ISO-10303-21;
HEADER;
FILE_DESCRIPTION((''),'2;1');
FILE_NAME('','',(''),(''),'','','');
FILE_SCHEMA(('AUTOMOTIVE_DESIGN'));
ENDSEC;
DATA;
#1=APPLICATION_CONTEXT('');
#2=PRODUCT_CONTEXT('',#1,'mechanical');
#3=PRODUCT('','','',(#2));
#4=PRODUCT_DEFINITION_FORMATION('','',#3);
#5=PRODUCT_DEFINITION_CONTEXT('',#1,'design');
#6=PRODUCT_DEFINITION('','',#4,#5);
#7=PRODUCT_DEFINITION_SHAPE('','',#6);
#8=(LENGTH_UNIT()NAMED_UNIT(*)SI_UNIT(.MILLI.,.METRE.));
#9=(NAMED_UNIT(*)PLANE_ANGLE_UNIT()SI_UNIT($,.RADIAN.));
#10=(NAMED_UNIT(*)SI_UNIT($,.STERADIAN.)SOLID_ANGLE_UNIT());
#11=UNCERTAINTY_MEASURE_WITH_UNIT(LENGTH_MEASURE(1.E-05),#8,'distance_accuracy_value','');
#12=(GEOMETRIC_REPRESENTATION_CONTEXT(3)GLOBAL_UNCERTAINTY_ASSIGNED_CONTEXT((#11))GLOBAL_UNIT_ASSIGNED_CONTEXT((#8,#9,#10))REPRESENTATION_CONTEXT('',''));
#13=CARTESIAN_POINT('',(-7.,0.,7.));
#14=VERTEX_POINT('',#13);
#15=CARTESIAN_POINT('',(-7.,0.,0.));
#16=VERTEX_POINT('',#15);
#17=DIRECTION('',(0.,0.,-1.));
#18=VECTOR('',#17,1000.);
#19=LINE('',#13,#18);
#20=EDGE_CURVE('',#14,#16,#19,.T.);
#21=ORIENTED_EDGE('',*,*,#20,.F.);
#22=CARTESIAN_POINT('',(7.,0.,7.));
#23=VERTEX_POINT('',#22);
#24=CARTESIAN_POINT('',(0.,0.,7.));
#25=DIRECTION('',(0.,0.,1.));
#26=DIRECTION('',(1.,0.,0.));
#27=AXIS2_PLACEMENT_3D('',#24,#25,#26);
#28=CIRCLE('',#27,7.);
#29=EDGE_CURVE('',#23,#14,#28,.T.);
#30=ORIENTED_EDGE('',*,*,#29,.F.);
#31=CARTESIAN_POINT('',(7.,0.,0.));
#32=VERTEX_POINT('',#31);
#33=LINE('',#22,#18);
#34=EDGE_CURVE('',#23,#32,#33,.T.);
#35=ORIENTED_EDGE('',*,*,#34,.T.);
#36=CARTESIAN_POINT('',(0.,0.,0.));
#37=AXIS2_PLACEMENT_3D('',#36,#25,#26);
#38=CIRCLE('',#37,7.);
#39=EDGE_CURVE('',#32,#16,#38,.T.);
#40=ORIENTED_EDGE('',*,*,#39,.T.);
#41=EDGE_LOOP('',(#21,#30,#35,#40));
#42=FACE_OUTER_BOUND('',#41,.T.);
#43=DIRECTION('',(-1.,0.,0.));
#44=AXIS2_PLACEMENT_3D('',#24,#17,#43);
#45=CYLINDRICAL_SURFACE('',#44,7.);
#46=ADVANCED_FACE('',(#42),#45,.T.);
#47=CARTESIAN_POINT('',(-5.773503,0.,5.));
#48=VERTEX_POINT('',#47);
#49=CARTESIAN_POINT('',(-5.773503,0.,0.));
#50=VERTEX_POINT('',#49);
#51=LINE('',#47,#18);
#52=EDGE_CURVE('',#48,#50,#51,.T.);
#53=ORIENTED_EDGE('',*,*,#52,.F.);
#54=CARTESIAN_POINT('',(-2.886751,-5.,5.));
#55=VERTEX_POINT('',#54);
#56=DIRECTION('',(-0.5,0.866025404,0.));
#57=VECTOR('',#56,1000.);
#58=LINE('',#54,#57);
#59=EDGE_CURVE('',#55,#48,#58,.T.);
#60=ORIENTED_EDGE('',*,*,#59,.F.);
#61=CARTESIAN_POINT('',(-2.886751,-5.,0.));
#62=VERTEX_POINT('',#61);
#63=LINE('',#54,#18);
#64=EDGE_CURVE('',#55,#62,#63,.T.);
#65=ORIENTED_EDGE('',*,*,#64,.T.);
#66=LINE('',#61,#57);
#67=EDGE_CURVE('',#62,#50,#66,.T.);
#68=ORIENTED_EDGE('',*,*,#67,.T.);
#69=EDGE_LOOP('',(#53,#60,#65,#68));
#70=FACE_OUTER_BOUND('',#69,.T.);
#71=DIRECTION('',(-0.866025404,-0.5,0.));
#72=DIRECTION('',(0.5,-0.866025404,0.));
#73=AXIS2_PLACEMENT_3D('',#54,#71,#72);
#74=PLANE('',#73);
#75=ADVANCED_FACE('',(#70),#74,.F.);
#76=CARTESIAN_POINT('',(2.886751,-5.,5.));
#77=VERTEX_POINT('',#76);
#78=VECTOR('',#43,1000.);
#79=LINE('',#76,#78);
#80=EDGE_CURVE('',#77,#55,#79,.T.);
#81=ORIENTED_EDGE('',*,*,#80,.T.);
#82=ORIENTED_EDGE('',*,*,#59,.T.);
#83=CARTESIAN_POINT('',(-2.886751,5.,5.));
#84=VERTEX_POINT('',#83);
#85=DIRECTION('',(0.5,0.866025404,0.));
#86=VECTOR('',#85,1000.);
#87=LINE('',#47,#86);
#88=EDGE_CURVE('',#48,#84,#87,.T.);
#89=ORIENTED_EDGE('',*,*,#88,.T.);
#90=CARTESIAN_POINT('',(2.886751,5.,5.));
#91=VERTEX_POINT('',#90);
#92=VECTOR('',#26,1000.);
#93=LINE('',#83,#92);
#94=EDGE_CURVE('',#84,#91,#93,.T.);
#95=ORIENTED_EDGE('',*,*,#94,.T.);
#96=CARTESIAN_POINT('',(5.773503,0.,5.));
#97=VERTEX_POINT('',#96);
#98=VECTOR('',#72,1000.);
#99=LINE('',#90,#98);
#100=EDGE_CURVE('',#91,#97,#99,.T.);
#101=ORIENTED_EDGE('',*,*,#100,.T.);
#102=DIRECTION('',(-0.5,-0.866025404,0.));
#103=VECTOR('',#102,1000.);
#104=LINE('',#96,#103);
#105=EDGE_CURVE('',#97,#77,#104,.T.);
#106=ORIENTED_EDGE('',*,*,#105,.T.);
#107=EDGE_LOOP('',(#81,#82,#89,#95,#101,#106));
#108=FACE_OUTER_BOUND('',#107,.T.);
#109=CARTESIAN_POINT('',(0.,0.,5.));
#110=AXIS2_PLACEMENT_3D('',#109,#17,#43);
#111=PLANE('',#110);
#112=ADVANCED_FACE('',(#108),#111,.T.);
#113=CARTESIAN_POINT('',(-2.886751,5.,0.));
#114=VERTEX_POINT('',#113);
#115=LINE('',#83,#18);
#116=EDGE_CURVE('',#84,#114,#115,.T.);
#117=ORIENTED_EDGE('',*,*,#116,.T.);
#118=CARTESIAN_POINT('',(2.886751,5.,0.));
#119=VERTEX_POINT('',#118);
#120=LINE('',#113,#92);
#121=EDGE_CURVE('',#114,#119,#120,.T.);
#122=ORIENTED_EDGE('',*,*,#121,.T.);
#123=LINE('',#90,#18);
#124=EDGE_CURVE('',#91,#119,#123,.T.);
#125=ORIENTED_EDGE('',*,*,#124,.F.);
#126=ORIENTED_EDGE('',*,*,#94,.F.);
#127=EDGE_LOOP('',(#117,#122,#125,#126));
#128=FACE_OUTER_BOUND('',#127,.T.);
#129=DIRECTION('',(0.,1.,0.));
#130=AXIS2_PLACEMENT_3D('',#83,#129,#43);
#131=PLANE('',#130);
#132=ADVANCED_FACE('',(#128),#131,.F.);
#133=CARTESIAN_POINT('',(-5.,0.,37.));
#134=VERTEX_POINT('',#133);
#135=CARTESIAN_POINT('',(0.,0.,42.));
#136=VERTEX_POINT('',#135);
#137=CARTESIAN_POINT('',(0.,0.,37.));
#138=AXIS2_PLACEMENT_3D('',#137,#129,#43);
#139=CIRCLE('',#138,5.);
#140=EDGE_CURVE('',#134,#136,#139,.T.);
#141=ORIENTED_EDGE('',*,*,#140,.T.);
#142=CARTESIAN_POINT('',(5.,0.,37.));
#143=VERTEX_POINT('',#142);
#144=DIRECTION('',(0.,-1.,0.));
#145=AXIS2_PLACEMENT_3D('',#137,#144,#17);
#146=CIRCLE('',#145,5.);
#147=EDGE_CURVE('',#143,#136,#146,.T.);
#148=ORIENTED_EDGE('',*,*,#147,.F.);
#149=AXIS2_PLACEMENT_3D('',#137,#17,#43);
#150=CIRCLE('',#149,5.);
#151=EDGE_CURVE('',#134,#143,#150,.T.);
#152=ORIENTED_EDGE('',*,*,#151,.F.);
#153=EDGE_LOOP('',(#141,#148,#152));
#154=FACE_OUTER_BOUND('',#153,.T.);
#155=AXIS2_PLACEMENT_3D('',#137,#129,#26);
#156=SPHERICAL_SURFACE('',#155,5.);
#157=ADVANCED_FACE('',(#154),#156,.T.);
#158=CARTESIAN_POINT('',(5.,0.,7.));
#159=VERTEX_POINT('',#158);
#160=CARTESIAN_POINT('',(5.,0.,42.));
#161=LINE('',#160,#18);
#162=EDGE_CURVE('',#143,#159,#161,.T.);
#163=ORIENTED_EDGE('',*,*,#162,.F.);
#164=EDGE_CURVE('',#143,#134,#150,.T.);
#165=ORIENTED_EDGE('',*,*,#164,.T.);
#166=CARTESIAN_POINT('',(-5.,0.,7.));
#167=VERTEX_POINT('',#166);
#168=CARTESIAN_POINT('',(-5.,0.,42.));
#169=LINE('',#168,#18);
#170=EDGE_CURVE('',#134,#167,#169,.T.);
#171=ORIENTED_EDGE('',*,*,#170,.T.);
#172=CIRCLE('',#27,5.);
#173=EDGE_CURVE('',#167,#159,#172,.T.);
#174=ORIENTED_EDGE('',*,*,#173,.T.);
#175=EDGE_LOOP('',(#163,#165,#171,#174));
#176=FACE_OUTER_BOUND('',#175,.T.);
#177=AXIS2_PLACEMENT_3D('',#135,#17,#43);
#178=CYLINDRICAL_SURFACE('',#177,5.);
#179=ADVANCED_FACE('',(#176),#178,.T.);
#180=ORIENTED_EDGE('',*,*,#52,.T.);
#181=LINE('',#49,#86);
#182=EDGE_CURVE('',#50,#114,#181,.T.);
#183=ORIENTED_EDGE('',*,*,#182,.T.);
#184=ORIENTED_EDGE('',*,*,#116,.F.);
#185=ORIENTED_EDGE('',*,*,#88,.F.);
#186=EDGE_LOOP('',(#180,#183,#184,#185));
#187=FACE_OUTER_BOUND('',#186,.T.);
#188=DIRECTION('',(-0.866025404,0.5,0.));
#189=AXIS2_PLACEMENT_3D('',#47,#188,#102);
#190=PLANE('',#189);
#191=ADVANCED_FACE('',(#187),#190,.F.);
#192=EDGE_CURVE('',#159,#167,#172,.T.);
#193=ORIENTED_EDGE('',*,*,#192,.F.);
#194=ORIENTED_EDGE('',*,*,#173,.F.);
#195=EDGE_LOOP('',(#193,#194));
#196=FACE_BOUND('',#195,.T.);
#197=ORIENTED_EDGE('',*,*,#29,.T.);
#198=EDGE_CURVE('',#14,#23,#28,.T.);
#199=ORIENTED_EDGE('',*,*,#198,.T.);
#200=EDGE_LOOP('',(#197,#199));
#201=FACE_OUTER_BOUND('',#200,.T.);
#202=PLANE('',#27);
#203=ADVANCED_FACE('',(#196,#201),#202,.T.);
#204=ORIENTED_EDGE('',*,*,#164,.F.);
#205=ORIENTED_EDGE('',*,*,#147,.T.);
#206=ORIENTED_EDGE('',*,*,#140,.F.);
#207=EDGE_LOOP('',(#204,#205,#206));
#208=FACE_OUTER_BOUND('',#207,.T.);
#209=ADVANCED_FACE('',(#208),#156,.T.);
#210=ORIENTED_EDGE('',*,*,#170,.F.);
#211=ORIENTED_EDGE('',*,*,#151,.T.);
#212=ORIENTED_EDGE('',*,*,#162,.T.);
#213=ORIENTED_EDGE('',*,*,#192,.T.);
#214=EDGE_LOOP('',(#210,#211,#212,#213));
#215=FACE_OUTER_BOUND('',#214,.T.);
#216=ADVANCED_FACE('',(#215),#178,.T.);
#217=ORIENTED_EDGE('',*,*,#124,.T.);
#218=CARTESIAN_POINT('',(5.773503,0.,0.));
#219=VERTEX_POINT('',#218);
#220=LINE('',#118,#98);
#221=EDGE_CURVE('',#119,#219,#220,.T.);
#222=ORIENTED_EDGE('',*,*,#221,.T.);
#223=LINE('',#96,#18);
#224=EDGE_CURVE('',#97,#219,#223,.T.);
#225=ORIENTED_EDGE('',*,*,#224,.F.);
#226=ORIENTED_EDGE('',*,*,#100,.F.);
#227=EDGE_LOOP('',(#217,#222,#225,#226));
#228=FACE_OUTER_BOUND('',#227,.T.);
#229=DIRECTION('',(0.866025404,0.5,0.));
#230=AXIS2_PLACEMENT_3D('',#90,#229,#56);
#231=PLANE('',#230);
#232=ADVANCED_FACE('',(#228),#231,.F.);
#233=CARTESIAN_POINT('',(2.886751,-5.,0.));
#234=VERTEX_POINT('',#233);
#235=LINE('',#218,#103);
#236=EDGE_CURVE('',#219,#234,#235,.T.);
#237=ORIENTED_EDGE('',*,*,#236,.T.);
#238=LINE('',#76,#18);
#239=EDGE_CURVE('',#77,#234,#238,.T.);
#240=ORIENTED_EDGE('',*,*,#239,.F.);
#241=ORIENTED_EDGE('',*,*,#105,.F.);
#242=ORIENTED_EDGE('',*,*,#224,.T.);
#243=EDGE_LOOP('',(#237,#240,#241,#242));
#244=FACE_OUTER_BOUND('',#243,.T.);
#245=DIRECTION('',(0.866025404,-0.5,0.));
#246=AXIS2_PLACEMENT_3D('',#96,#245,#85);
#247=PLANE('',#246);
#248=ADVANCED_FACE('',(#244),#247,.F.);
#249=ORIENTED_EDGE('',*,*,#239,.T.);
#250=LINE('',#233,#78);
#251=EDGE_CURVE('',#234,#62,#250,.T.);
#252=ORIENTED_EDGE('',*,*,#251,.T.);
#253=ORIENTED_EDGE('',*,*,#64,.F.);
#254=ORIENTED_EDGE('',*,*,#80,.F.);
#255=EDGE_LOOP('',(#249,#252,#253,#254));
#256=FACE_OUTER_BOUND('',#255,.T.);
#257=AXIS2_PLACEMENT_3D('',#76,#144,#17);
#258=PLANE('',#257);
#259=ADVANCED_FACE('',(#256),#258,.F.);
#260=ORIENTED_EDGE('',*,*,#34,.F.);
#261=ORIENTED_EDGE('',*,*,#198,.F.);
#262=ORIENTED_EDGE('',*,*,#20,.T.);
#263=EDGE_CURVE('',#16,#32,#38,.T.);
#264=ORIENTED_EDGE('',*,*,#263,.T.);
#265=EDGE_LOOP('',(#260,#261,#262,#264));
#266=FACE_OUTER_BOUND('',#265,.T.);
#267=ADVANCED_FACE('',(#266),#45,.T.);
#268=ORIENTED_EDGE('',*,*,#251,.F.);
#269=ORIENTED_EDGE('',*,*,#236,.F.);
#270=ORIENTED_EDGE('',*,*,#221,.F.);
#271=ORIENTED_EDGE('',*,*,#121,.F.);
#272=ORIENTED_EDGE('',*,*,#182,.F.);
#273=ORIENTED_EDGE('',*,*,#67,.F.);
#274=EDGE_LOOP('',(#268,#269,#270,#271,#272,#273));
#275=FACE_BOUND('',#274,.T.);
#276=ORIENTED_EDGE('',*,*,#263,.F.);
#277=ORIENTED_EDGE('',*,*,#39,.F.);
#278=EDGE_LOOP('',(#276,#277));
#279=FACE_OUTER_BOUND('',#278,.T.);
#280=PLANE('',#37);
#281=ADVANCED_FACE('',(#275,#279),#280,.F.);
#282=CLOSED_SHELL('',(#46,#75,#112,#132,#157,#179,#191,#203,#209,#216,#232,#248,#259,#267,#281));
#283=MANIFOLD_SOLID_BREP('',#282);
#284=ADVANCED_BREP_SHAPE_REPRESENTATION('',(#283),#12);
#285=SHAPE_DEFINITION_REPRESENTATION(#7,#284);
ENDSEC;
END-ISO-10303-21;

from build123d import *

# Parameters (mm, degrees)
HEAD_PROFILE_SKETCH_R       = 7
HEAD_14X10_DEPTH            = 7
SHANK_PROFILE_SKETCH_R      = 5
SHANK_10X35_DEPTH           = 35
DOMED_END_R5_R              = 5
HEX_SOCKET_CUT_5_DEEP_DEPTH = 5


with BuildPart() as part:
    # Head Profile Sketch → Head Ø14x10 (new body)
    with BuildSketch(Plane.XY):
        Circle(HEAD_PROFILE_SKETCH_R)
    extrude(amount=HEAD_14X10_DEPTH)

    # Shank Profile Sketch → Shank Ø10x35 (add)
    with BuildSketch(Plane.XY.offset(7)):
        Circle(SHANK_PROFILE_SKETCH_R)
    extrude(amount=SHANK_10X35_DEPTH)

    # Domed End R5
    domed_end_r5_edges = [part.edges().sort_by_distance(p)[0] for p in [
        (-5, 0, 42),
    ]]
    fillet(domed_end_r5_edges, radius=DOMED_END_R5_R)

    # Hex Socket Sketch → Hex Socket Cut 5 Deep (cut)
    with BuildSketch(Plane(origin=(0, 0, 0), x_dir=(-1, 0, 0), z_dir=(0, 0, -1))):
        Polygon((5.773502692, 0), (2.886751346, 5), (-2.886751346, 5), (-5.773502692, 0), (-2.886751346, -5), (2.886751346, -5), align=None)
    extrude(amount=-HEX_SOCKET_CUT_5_DEEP_DEPTH, mode=Mode.SUBTRACT)


solid = part.part
